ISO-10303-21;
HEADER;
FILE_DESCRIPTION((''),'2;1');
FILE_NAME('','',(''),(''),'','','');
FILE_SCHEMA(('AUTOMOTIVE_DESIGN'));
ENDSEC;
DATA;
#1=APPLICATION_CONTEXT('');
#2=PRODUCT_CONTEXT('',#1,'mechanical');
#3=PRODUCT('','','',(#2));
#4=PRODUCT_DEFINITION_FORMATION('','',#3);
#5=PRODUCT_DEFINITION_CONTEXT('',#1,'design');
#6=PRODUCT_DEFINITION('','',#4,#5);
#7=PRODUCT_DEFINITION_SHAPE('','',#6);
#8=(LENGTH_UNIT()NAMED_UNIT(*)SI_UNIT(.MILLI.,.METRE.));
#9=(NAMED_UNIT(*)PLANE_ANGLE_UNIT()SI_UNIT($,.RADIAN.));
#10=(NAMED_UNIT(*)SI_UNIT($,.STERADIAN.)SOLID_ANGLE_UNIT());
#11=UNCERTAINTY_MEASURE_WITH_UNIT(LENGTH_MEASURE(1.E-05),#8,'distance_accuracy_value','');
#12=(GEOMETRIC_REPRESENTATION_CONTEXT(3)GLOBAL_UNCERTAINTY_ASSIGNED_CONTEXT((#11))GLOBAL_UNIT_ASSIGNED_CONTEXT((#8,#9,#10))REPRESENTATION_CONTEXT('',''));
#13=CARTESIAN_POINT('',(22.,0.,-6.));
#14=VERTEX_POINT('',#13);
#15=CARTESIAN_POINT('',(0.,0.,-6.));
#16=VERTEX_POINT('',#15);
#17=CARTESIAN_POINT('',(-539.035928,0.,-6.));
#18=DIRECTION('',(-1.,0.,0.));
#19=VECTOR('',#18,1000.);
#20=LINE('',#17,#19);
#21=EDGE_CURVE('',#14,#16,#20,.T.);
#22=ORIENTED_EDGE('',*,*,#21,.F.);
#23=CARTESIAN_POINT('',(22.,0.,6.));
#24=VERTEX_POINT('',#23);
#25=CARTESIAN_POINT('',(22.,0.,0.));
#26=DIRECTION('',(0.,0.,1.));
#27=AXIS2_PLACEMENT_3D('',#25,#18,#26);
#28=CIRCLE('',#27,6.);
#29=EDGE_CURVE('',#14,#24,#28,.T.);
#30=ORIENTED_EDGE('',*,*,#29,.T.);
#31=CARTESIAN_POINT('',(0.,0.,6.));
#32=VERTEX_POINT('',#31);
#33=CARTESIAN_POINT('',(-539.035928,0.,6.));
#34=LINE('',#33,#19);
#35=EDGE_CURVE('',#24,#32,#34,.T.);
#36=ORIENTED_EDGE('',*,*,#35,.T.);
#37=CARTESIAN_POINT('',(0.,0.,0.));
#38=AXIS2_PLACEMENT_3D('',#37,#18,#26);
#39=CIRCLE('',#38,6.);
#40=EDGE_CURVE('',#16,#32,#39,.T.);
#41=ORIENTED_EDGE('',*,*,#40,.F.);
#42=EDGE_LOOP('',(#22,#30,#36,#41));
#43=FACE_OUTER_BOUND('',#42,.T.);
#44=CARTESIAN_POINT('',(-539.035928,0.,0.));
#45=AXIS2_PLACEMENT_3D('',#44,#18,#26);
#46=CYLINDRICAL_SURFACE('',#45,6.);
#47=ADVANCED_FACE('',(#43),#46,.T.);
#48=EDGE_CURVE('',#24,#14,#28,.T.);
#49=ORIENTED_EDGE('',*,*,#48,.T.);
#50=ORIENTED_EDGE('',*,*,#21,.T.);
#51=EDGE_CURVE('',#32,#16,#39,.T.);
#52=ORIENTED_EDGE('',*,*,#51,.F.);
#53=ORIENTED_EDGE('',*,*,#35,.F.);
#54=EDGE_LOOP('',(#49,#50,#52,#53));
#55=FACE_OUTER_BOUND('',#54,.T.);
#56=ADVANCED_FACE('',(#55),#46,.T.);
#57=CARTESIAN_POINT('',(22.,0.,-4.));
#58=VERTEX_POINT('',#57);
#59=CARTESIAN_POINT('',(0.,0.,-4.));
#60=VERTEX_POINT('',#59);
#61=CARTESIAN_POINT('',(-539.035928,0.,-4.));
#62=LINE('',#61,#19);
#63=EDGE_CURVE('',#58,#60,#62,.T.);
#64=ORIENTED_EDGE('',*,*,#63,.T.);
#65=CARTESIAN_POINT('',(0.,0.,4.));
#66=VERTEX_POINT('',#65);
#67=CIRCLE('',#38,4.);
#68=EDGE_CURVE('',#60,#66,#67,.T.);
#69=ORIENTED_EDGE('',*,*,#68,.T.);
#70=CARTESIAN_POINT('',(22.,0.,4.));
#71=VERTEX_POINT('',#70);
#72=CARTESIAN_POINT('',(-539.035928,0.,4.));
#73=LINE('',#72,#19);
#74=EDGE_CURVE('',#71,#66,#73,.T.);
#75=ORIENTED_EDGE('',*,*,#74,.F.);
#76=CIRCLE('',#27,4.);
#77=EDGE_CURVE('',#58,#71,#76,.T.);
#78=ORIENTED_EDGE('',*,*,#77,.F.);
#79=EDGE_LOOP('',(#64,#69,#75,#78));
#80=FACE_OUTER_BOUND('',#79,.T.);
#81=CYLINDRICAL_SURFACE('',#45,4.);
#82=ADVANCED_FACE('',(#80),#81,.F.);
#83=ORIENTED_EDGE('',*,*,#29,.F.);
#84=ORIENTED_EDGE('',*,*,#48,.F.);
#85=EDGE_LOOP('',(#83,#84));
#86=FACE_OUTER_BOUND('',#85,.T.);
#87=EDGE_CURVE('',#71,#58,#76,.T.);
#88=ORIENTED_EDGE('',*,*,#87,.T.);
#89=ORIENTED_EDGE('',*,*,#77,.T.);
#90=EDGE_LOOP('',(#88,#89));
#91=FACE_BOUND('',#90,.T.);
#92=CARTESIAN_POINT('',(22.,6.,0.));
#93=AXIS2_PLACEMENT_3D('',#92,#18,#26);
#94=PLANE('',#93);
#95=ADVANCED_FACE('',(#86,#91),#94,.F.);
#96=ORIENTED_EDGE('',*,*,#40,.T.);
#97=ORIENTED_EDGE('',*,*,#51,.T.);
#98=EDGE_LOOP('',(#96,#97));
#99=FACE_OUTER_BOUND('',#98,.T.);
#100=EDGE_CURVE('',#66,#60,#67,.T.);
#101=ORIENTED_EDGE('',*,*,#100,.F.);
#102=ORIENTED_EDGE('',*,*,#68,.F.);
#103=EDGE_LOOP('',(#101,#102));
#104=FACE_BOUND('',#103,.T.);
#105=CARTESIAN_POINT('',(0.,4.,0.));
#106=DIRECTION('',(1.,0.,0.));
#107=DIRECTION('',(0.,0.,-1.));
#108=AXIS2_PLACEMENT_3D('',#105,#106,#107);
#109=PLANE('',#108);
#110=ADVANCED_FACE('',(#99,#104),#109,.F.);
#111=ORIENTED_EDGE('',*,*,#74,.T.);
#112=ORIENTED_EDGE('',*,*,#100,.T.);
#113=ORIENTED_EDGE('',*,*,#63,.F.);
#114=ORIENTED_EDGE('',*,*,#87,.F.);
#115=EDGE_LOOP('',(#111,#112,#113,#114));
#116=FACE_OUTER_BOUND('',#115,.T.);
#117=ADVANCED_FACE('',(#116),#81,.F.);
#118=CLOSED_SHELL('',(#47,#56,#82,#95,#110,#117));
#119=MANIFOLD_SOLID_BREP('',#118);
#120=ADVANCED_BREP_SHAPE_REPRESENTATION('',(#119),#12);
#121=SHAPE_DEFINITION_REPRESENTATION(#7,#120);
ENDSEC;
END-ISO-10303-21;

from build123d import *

# Parameters (mm, degrees)
SKETCH_1_W = 22
SKETCH_1_H = 2


with BuildPart() as part:
    # 草图1 → 旋转1 (revolve)
    with BuildSketch(Plane.XY, mode=Mode.PRIVATE) as revolve_1_sk:
        with Locations((11, 5)):
            Rectangle(SKETCH_1_W, SKETCH_1_H)
    revolve(revolve_1_sk.sketch.rotate(Axis((-539.035928085, 0, 0), (1, 0, 0)), 90), axis=Axis((-539.035928085, 0, 0), (1, 0, 0)))


solid = part.part
